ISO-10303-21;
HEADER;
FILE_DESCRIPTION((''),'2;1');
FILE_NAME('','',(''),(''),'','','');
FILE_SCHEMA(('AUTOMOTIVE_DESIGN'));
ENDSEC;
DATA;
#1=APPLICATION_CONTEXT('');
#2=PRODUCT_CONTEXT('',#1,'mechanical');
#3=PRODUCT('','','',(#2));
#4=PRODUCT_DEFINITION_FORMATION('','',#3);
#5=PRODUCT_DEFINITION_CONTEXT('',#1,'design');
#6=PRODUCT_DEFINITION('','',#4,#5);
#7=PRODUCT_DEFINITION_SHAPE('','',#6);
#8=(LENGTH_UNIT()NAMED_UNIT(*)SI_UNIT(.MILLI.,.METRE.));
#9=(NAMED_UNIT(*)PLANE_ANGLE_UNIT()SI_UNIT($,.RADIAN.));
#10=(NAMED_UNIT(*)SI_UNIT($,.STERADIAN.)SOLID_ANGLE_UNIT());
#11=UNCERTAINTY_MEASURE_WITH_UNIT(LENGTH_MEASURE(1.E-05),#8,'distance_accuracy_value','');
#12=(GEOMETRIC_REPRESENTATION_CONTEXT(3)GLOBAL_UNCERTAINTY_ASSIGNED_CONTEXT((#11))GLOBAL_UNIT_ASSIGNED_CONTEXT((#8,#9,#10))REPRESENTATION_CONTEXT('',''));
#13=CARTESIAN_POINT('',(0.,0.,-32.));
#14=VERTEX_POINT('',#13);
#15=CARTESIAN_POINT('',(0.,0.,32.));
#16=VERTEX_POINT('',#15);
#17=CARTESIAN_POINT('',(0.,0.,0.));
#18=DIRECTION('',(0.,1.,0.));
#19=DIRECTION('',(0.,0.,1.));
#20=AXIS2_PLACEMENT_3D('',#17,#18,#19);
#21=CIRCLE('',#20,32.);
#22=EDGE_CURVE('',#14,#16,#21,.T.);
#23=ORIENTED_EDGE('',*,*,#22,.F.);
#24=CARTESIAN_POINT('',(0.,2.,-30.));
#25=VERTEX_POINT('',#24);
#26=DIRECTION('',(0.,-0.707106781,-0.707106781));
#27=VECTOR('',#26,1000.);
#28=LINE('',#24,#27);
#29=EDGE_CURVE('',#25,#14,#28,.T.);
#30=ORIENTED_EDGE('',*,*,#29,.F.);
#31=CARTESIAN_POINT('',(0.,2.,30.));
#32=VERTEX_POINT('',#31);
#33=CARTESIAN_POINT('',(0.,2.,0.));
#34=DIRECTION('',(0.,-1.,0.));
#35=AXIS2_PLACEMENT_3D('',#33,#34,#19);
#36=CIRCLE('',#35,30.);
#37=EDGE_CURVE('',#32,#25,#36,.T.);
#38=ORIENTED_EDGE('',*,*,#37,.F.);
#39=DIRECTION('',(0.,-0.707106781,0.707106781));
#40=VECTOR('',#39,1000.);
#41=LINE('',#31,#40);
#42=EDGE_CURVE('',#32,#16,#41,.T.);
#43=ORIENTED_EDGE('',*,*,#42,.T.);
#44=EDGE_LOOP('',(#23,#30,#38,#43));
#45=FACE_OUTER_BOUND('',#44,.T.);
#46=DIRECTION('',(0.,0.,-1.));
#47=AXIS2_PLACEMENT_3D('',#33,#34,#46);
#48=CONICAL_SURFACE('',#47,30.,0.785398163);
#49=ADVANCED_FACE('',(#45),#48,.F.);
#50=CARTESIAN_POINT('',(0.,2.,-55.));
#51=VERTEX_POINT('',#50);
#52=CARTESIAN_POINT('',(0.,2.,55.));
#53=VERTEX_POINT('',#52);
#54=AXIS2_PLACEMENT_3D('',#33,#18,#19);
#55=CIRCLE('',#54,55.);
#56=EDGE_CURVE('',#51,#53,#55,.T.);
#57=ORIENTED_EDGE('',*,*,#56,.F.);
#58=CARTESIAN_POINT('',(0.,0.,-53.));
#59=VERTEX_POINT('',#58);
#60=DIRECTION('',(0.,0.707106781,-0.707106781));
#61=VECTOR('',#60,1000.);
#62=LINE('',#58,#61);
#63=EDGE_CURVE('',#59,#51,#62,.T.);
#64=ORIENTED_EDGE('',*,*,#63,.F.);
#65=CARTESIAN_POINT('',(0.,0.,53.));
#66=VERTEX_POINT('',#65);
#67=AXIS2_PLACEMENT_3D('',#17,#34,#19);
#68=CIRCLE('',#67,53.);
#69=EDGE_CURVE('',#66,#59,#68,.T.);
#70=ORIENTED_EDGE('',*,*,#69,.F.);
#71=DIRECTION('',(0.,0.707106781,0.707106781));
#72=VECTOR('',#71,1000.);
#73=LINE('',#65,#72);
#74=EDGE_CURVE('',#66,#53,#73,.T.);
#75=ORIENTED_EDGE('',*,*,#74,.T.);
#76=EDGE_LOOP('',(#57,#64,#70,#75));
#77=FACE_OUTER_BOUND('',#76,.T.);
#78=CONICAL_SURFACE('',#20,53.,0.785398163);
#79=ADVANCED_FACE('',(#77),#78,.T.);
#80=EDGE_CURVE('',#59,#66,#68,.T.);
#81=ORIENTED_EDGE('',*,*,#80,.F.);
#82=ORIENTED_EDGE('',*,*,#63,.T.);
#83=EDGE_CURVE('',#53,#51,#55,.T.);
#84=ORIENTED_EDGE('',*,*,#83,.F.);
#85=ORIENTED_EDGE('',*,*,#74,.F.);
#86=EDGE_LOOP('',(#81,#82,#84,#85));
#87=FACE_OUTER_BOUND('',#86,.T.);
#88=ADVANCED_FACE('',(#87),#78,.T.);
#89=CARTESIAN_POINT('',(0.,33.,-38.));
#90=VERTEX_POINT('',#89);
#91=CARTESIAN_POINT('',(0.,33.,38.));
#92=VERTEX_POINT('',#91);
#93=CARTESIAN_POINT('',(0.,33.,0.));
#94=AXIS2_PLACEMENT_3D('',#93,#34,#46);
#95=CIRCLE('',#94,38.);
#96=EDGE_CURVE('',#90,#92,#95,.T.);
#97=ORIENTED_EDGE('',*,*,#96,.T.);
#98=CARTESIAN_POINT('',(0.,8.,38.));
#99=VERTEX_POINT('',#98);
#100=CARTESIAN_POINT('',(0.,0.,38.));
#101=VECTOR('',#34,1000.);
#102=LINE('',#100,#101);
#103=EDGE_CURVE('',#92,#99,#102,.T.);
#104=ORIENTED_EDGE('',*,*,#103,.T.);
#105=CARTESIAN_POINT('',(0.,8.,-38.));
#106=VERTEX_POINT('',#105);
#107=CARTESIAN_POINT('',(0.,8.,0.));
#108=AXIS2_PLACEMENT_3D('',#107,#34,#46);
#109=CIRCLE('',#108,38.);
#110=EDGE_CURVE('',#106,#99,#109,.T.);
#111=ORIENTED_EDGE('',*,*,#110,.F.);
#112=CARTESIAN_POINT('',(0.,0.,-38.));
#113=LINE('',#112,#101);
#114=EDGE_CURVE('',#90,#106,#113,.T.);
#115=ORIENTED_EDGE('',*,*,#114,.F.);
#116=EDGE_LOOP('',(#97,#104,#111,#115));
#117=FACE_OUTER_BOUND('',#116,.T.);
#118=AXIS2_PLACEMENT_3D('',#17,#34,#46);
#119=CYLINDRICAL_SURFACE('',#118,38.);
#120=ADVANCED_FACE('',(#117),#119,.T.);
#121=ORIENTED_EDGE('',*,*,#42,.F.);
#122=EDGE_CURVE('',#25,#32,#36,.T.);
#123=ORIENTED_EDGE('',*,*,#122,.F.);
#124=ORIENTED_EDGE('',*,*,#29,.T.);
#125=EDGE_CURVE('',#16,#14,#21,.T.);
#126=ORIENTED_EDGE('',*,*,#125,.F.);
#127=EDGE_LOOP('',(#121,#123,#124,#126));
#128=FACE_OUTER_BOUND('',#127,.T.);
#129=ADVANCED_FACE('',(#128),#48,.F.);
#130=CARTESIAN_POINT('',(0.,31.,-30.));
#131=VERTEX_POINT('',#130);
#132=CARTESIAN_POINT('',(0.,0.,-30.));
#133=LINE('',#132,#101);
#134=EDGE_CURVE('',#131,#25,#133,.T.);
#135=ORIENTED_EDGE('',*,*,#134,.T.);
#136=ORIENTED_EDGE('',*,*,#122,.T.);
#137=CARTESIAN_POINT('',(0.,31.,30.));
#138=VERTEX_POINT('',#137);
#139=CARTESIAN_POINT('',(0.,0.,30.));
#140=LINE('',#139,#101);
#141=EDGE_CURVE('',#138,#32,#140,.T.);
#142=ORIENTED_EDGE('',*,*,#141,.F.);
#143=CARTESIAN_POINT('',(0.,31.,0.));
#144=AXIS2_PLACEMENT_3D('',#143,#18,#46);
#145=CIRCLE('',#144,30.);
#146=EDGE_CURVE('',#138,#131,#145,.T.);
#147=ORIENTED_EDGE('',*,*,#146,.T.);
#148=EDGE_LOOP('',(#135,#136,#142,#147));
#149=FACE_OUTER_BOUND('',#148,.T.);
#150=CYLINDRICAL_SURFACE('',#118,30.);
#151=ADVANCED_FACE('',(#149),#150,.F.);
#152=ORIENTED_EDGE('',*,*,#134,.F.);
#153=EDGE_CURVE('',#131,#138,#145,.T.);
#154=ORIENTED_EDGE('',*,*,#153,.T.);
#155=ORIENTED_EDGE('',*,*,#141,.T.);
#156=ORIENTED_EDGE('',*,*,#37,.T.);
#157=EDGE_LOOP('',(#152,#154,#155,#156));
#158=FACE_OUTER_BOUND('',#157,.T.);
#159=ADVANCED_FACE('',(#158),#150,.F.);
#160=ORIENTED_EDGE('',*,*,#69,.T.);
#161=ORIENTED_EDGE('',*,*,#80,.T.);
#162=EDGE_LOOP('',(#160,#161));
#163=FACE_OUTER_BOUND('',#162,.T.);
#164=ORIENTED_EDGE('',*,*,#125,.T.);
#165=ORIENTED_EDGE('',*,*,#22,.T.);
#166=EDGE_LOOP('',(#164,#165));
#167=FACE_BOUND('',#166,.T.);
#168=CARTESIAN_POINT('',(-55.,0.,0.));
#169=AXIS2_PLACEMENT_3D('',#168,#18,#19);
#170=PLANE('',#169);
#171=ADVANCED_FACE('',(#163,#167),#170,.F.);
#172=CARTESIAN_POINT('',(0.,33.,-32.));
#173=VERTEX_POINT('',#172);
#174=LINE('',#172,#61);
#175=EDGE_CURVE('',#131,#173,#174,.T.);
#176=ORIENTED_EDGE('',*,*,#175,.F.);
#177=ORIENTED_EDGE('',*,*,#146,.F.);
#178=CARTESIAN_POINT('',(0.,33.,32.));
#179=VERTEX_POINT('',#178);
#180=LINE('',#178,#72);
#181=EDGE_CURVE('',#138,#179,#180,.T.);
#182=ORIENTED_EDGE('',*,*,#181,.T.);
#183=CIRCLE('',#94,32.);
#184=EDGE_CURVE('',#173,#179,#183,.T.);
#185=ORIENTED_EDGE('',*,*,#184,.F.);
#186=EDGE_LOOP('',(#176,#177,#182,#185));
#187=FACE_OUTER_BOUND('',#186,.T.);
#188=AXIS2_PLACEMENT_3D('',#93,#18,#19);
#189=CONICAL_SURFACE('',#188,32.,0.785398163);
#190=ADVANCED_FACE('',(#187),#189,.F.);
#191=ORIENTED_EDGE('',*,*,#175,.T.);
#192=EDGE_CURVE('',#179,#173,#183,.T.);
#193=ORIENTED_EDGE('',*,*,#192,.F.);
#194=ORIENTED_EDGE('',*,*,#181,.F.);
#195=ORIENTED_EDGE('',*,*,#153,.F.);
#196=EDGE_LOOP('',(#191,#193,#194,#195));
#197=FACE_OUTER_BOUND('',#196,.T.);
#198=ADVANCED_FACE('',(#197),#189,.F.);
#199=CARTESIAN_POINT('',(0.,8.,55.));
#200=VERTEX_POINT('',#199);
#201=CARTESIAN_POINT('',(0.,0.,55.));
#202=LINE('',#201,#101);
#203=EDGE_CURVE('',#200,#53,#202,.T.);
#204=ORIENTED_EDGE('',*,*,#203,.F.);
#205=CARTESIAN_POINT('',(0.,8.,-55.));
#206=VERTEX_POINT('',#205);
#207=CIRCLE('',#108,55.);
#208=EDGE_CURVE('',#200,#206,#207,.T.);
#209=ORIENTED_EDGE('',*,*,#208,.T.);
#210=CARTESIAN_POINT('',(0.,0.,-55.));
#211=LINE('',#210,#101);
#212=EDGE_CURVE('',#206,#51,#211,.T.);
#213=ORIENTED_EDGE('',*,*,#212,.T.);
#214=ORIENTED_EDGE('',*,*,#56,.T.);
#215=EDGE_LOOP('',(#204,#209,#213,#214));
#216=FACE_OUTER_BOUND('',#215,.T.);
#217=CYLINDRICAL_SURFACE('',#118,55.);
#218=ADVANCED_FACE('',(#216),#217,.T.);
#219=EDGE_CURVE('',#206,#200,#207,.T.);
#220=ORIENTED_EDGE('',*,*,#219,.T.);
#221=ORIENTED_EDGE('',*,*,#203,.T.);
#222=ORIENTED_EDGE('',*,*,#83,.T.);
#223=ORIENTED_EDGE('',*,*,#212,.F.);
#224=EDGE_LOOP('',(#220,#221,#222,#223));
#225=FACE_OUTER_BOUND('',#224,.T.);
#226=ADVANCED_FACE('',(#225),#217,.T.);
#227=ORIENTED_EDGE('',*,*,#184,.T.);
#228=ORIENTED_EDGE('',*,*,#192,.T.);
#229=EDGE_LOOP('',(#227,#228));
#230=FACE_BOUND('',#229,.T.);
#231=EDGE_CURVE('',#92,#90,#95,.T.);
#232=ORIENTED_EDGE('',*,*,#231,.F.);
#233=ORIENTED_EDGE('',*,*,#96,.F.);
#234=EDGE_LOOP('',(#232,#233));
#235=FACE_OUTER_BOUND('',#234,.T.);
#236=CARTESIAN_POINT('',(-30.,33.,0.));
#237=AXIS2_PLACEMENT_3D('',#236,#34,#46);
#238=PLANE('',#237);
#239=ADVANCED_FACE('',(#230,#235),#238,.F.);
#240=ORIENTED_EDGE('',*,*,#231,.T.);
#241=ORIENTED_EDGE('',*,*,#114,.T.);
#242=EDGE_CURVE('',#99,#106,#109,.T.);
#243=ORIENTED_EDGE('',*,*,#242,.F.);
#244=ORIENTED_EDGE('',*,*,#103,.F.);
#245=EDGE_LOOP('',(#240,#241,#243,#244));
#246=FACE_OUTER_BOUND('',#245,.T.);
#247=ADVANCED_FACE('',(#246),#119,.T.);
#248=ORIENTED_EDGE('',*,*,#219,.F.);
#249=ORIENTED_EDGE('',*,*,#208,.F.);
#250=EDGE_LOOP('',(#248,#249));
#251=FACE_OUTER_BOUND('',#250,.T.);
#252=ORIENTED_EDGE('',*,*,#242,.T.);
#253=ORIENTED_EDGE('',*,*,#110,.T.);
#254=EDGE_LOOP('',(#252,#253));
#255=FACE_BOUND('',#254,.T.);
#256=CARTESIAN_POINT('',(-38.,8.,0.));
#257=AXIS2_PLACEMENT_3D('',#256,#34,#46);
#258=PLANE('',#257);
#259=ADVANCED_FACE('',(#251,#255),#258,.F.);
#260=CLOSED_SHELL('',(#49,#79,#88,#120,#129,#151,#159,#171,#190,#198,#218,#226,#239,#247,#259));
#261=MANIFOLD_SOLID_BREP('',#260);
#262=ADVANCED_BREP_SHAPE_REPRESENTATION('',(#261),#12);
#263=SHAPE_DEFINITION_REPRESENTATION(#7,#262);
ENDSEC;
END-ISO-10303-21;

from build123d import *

# Parameters (mm, degrees)
CHAMFER1_SIZE = 2


with BuildPart() as part:
    # Sketch1 → Revolve1 (revolve)
    with BuildSketch(Plane.XY, mode=Mode.PRIVATE) as revolve1_sk:
        Polygon((-30, 0), (-30, 33), (-38, 33), (-38, 8), (-55, 8), (-55, 0), align=None)
    revolve(revolve1_sk.sketch.rotate(Axis((0, 0, 0), (0, 1, 0)), 270), axis=Axis((0, 0, 0), (0, 1, 0)))

    # Chamfer1
    chamfer1_edges = [part.edges().sort_by_distance(p)[0] for p in [
        (0, 0, 55),
        (0, 33, 30),
        (0, 0, 30),
    ]]
    chamfer(chamfer1_edges, length=CHAMFER1_SIZE)


solid = part.part
